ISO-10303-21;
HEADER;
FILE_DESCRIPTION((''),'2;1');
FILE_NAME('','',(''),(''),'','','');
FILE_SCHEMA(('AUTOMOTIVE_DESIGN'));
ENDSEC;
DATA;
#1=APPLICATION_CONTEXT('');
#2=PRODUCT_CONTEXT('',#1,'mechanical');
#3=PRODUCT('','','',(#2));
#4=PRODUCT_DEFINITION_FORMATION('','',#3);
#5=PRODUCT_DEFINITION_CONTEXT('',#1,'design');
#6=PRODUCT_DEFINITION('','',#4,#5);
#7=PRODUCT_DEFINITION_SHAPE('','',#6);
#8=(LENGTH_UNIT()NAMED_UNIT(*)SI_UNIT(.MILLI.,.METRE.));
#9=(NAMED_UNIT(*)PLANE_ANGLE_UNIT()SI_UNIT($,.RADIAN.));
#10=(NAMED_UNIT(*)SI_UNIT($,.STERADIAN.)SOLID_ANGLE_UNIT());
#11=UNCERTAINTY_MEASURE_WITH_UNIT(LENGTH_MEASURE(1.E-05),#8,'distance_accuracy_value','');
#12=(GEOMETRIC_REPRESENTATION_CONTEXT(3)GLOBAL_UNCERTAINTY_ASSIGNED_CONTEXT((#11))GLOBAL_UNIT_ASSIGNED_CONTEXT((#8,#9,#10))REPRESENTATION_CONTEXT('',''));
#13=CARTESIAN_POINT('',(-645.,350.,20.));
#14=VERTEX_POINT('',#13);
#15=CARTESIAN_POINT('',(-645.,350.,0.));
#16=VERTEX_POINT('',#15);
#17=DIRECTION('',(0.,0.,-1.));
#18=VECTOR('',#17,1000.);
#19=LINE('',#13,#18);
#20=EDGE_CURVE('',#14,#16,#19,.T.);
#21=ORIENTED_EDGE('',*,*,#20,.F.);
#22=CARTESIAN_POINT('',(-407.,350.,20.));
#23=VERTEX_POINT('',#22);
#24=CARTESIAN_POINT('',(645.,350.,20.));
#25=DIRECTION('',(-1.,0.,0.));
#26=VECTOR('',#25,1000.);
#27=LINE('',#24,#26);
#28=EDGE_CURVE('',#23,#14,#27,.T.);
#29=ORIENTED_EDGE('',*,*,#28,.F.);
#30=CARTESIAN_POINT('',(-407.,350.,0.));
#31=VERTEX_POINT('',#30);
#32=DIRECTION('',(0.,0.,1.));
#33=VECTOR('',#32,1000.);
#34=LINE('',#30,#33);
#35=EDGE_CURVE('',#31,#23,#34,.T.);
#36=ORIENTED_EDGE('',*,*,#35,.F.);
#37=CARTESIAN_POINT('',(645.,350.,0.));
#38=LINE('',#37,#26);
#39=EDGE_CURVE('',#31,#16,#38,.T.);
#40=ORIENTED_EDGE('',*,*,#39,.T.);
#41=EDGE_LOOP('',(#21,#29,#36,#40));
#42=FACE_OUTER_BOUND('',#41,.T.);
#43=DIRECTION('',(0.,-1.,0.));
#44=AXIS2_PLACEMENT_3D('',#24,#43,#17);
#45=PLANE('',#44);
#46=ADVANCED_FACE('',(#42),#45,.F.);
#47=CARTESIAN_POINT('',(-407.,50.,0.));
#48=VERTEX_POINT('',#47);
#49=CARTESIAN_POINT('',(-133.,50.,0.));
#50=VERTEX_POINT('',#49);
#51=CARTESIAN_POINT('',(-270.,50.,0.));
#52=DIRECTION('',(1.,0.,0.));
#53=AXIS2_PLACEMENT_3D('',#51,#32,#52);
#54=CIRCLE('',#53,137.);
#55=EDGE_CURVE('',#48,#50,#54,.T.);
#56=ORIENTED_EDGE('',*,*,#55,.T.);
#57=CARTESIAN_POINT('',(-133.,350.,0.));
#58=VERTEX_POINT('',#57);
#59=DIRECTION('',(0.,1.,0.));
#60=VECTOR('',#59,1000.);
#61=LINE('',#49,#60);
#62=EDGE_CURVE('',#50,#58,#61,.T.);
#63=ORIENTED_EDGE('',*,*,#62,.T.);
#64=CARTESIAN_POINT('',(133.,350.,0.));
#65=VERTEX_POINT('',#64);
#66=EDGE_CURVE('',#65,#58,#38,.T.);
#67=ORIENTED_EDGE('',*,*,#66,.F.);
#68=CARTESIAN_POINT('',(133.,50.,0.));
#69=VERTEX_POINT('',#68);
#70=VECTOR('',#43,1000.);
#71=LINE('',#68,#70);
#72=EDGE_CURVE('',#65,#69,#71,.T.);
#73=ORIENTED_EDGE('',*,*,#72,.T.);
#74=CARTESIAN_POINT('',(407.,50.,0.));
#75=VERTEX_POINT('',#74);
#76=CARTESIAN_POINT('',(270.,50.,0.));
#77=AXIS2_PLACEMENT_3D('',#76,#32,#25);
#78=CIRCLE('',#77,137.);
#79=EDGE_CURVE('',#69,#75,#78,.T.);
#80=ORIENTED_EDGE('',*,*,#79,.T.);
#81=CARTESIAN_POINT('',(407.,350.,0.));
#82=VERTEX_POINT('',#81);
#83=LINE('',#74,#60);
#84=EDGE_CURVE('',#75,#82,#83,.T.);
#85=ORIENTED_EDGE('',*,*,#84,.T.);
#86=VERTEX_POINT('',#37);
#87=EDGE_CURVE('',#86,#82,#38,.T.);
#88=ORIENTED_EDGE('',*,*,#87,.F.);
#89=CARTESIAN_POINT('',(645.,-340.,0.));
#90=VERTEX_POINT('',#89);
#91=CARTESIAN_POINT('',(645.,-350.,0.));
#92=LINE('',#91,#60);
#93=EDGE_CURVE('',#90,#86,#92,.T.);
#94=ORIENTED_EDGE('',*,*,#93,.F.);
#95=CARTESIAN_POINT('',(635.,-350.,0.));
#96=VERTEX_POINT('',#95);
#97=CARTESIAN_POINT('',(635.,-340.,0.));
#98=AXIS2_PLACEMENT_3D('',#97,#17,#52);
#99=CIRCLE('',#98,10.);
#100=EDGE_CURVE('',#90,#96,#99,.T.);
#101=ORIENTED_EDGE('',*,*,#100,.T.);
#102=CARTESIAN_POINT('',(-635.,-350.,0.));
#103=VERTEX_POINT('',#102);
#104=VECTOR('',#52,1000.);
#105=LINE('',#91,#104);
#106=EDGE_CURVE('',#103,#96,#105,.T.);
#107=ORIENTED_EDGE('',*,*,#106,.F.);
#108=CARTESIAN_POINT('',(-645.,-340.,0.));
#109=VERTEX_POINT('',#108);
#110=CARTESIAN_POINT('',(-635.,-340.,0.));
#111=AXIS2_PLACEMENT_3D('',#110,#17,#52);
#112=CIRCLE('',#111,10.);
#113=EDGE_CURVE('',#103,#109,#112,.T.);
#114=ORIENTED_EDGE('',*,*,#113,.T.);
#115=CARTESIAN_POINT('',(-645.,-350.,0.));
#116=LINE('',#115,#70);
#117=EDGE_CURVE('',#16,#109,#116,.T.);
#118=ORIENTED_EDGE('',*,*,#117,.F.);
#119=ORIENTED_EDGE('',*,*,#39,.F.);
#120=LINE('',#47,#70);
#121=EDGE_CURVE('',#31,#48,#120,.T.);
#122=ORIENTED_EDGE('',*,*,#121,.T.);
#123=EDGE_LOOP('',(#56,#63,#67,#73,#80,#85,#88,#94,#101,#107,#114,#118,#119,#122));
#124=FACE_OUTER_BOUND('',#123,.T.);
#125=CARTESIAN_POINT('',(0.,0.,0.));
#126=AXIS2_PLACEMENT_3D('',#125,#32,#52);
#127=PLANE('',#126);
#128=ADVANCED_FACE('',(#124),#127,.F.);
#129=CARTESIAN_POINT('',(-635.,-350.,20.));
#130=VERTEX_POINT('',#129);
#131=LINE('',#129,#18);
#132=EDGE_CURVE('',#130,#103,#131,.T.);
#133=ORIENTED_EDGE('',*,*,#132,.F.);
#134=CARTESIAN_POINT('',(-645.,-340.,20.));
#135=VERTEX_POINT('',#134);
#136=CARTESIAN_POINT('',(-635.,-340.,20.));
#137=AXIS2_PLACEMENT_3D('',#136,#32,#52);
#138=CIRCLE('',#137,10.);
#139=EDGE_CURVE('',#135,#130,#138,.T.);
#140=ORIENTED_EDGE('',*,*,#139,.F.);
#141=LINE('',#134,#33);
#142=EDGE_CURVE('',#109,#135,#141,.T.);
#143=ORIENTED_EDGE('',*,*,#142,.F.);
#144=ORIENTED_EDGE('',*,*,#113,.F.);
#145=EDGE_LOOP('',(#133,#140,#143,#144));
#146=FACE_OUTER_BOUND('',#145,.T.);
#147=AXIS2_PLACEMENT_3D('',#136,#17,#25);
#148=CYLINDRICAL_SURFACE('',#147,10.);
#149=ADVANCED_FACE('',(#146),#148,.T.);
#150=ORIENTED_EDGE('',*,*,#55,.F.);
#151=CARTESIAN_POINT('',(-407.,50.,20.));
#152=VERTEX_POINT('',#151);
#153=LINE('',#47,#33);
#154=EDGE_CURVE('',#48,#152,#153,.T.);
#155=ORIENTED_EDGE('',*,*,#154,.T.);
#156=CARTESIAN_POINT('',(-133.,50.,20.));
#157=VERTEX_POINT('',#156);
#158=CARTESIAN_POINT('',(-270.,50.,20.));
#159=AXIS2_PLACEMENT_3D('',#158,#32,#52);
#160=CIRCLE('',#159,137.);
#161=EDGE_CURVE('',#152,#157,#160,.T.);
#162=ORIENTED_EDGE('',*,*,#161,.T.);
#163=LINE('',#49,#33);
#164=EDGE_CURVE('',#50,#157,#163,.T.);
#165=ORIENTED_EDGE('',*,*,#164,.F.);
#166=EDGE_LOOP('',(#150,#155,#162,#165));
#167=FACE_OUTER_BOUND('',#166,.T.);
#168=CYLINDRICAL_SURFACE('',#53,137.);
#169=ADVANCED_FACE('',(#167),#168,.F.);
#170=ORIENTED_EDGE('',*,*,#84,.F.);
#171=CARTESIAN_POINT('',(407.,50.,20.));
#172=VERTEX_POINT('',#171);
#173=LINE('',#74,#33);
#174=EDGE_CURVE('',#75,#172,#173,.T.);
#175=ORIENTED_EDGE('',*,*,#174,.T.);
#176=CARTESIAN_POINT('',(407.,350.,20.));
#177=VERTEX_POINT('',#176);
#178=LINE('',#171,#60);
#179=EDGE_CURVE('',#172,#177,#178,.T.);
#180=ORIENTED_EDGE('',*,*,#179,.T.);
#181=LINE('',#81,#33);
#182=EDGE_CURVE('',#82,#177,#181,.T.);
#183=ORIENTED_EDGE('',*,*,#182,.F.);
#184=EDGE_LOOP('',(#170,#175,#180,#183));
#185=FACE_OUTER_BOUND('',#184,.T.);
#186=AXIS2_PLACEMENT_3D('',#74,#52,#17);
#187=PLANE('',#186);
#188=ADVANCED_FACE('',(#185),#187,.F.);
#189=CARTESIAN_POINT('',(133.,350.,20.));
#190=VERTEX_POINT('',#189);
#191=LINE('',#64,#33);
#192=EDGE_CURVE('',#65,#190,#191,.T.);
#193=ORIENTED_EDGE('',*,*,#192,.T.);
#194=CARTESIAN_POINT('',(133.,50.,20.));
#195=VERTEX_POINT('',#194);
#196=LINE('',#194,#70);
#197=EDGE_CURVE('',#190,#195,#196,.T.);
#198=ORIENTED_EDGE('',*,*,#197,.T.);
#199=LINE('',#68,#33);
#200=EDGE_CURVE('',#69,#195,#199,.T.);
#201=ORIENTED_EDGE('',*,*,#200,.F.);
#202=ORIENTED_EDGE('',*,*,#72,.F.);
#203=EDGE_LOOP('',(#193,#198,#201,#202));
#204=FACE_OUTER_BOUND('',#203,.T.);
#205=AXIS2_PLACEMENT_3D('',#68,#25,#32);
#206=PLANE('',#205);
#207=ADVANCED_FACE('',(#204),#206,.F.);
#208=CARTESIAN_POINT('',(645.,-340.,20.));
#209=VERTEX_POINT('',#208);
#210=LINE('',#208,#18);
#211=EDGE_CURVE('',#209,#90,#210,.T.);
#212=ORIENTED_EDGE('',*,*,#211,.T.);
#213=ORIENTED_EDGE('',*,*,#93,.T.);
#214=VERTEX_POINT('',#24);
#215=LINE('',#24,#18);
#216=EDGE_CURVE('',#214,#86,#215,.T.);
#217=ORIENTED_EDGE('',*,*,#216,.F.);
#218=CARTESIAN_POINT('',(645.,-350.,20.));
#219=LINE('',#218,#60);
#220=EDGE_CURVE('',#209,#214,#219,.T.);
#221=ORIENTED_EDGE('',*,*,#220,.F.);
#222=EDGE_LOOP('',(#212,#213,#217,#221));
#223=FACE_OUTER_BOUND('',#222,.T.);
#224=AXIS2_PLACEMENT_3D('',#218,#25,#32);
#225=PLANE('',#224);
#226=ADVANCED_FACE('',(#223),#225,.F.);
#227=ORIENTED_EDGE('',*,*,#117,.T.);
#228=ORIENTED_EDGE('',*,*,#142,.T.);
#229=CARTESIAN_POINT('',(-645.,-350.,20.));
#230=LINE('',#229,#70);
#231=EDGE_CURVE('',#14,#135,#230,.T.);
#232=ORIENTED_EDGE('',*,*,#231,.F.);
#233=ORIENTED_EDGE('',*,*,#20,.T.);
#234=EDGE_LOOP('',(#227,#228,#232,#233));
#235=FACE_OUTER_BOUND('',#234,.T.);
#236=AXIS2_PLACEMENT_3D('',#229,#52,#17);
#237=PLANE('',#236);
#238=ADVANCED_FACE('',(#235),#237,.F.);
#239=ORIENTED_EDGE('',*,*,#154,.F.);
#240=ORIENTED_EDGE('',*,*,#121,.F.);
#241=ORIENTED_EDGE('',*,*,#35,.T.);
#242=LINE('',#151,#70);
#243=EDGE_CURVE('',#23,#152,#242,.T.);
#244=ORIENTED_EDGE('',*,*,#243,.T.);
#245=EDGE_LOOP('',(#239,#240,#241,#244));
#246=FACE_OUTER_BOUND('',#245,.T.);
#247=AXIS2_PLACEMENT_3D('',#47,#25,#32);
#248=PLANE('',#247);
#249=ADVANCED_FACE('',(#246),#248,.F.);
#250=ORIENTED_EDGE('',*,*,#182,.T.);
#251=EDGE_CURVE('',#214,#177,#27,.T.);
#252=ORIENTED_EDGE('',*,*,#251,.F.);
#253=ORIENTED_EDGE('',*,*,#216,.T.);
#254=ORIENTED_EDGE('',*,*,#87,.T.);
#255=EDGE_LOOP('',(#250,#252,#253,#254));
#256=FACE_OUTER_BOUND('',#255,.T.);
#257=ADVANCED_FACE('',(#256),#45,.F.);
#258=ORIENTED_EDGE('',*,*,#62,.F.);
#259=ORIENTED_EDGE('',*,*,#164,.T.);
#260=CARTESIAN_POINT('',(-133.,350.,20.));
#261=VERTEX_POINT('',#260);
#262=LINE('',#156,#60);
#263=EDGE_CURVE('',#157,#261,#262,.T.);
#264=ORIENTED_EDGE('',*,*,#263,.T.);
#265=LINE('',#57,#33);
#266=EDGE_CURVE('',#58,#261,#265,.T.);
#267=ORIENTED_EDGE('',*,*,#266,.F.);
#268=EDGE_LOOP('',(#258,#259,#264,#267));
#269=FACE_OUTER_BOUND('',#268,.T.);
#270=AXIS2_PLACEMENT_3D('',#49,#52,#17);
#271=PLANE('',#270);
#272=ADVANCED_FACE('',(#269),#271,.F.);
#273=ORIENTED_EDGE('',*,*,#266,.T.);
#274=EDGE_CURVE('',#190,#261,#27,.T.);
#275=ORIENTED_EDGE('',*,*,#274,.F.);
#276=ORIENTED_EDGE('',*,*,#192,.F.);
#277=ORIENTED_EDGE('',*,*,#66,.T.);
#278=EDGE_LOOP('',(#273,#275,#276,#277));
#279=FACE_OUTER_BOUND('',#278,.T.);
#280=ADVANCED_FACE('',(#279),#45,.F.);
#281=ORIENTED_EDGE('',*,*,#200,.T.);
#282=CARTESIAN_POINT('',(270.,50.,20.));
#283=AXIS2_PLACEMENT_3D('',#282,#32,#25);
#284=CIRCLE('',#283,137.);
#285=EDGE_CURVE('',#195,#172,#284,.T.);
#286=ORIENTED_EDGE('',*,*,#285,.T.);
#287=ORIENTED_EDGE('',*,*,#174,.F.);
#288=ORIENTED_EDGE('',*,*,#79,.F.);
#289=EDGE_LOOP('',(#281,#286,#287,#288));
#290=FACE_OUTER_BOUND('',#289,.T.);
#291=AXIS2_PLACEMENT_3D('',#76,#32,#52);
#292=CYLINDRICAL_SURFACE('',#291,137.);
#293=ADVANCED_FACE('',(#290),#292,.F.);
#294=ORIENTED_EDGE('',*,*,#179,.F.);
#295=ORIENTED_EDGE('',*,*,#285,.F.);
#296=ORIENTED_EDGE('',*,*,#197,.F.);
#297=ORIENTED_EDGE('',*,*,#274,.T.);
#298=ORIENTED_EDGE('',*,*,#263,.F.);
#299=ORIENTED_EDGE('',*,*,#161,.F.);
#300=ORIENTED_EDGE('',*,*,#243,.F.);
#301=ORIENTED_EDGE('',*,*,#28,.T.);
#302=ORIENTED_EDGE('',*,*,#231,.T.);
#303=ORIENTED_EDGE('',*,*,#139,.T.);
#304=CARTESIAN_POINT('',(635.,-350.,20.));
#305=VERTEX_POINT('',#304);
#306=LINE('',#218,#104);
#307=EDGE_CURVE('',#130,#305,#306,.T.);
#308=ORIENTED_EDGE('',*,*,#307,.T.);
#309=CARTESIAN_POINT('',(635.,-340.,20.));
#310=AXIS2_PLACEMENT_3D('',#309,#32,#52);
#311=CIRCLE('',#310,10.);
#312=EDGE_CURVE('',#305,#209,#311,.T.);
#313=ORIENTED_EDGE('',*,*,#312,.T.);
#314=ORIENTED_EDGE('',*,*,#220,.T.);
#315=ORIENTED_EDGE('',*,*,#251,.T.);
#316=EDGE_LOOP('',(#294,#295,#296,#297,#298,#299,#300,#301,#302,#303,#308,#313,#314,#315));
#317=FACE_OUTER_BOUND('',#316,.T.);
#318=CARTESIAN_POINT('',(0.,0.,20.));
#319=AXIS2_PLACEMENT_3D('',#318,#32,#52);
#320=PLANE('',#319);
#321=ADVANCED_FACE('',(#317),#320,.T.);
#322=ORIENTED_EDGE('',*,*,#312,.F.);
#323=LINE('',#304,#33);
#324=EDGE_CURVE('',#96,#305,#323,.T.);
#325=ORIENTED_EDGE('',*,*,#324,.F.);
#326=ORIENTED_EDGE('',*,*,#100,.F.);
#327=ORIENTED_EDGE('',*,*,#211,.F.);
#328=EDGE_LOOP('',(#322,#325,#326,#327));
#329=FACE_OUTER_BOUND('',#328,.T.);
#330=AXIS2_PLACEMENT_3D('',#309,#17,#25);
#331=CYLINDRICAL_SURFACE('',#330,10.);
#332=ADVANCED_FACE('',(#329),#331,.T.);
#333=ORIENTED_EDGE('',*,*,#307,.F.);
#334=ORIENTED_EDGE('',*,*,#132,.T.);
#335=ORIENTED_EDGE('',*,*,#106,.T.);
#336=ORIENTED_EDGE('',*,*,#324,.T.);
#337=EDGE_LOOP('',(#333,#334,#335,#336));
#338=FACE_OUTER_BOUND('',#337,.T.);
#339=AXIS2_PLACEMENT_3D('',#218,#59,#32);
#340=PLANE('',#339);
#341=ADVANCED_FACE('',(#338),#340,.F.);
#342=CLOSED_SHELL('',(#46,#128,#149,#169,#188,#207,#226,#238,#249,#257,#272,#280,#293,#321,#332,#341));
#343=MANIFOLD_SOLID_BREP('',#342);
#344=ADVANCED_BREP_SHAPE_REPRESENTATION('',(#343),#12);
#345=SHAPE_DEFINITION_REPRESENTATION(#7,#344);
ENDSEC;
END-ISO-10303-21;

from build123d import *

# Parameters (mm, degrees)
SKETCH1_W           = 1290
SKETCH1_H           = 700
BOSS_EXTRUDE1_DEPTH = 20
CUT_EXTRUDE1_DEPTH  = 20
FILLET1_R           = 10


with BuildPart() as part:
    # Sketch1 → Boss-Extrude1 (new body)
    with BuildSketch(Plane.XY):
        Rectangle(SKETCH1_W, SKETCH1_H)
    extrude(amount=BOSS_EXTRUDE1_DEPTH)

    # Sketch2 → Cut-Extrude1 (cut)
    with BuildSketch(Plane.XY.offset(20)):
        with BuildLine():
            Line((-407, 50), (-407, 350))
            Line((-407, 350), (-133, 350))
            Line((-133, 350), (-133, 50))
            ThreePointArc((-133, 50), (-270, -87), (-407, 50))
        make_face()
        with BuildLine():
            Line((407, 350), (133, 350))
            Line((133, 350), (133, 50))
            ThreePointArc((133, 50), (270, -87), (407, 50))
            Line((407, 50), (407, 350))
        make_face()
    extrude(amount=-CUT_EXTRUDE1_DEPTH, mode=Mode.SUBTRACT)

    # Fillet1
    fillet1_edges = [part.edges().sort_by_distance(p)[0] for p in [
        (645, -350, 10),
        (-645, -350, 10),
    ]]
    fillet(fillet1_edges, radius=FILLET1_R)


solid = part.part
